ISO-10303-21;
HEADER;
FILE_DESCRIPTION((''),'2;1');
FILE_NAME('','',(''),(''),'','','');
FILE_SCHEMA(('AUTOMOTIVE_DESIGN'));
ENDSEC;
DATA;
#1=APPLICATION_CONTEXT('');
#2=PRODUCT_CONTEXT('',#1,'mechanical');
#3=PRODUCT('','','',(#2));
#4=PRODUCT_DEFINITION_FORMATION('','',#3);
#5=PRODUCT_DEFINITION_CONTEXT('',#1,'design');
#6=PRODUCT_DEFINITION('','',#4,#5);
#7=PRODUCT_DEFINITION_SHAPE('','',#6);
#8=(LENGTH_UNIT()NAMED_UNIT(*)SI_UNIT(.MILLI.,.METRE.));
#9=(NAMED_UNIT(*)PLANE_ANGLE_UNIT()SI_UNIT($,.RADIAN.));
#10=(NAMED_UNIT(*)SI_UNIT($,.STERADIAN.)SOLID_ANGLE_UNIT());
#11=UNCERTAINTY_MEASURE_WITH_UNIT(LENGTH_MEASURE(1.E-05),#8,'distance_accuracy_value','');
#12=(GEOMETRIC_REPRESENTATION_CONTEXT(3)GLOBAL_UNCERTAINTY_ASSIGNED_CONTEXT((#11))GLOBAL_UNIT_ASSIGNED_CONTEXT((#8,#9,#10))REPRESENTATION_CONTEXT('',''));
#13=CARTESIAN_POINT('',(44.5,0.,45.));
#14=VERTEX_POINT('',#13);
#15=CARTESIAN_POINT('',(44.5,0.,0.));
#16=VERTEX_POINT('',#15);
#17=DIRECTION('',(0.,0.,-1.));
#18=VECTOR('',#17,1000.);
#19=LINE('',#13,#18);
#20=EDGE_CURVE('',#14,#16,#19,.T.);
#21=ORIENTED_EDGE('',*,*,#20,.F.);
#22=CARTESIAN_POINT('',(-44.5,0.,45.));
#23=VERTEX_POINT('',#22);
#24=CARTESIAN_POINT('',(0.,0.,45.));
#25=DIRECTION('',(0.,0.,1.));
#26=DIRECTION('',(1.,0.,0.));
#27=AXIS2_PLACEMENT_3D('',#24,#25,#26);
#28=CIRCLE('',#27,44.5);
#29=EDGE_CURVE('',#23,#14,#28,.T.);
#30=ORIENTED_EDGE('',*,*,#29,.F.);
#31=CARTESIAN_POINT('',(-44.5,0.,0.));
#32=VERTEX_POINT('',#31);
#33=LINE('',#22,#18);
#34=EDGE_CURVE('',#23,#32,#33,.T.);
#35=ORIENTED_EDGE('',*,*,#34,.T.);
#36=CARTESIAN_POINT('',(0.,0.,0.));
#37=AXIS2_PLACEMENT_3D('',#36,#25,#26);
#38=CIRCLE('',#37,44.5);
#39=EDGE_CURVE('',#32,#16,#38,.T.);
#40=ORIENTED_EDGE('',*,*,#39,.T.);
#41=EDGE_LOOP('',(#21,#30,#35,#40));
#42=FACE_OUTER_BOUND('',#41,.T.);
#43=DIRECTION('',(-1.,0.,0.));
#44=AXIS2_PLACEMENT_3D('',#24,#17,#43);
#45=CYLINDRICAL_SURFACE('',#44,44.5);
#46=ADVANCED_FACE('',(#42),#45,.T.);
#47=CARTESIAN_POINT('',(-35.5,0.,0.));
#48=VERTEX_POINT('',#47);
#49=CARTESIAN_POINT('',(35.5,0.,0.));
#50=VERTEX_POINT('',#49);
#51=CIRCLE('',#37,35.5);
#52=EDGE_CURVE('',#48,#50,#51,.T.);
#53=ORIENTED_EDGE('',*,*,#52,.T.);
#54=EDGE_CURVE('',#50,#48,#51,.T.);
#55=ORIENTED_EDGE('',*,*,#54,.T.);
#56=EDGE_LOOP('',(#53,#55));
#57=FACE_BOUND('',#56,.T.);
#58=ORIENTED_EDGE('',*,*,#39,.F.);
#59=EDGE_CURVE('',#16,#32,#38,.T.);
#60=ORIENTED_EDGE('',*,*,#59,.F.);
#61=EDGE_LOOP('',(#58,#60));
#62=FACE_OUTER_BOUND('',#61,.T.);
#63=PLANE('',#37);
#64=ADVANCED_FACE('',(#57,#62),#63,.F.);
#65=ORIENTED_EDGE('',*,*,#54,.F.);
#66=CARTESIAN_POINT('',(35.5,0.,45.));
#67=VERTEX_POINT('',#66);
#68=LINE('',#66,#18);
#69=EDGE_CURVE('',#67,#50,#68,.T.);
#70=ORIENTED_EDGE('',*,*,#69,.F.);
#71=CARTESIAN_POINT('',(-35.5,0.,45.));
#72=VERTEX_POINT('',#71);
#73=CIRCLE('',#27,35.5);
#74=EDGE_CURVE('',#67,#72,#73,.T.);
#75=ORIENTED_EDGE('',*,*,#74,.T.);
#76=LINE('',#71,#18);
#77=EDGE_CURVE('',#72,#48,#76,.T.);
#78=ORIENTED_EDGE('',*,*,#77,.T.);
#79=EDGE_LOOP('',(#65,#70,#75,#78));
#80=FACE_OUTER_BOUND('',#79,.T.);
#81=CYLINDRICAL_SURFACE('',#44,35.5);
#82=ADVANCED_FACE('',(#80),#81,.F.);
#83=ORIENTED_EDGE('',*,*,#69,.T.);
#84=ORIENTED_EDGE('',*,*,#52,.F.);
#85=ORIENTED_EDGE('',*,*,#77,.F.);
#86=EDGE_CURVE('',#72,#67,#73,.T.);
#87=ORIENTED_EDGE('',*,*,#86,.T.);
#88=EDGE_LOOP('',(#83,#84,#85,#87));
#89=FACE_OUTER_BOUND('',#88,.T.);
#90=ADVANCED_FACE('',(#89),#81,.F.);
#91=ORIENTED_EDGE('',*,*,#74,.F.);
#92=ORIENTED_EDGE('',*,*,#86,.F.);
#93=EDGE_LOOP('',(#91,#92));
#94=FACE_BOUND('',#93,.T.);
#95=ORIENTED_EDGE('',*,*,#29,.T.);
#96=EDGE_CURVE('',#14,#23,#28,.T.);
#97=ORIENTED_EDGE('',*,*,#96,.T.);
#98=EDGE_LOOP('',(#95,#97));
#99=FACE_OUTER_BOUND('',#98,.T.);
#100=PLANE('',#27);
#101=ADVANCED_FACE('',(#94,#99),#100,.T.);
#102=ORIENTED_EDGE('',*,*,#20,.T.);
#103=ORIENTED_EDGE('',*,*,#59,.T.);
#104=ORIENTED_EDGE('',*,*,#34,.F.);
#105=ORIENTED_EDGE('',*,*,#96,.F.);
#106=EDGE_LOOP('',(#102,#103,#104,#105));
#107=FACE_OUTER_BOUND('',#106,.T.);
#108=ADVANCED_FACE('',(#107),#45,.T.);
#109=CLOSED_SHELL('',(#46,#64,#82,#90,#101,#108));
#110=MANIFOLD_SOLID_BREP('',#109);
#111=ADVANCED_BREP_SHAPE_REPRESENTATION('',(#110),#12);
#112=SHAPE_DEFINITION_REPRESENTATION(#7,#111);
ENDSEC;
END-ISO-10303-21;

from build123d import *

# Parameters (mm, degrees)
SKETCH1_R           = 44.5
SKETCH1_R_2         = 35.5
BOSS_EXTRUDE1_DEPTH = 45


with BuildPart() as part:
    # Sketch1 → Boss-Extrude1 (new body)
    with BuildSketch(Plane.XY):
        with Locations(Location((0, 0, 0), (0, 0, 180))):
            Circle(SKETCH1_R)
        with Locations(Location((0, 0, 0), (0, 0, 180))):
            Circle(SKETCH1_R_2, mode=Mode.SUBTRACT)
    extrude(amount=BOSS_EXTRUDE1_DEPTH)


solid = part.part
